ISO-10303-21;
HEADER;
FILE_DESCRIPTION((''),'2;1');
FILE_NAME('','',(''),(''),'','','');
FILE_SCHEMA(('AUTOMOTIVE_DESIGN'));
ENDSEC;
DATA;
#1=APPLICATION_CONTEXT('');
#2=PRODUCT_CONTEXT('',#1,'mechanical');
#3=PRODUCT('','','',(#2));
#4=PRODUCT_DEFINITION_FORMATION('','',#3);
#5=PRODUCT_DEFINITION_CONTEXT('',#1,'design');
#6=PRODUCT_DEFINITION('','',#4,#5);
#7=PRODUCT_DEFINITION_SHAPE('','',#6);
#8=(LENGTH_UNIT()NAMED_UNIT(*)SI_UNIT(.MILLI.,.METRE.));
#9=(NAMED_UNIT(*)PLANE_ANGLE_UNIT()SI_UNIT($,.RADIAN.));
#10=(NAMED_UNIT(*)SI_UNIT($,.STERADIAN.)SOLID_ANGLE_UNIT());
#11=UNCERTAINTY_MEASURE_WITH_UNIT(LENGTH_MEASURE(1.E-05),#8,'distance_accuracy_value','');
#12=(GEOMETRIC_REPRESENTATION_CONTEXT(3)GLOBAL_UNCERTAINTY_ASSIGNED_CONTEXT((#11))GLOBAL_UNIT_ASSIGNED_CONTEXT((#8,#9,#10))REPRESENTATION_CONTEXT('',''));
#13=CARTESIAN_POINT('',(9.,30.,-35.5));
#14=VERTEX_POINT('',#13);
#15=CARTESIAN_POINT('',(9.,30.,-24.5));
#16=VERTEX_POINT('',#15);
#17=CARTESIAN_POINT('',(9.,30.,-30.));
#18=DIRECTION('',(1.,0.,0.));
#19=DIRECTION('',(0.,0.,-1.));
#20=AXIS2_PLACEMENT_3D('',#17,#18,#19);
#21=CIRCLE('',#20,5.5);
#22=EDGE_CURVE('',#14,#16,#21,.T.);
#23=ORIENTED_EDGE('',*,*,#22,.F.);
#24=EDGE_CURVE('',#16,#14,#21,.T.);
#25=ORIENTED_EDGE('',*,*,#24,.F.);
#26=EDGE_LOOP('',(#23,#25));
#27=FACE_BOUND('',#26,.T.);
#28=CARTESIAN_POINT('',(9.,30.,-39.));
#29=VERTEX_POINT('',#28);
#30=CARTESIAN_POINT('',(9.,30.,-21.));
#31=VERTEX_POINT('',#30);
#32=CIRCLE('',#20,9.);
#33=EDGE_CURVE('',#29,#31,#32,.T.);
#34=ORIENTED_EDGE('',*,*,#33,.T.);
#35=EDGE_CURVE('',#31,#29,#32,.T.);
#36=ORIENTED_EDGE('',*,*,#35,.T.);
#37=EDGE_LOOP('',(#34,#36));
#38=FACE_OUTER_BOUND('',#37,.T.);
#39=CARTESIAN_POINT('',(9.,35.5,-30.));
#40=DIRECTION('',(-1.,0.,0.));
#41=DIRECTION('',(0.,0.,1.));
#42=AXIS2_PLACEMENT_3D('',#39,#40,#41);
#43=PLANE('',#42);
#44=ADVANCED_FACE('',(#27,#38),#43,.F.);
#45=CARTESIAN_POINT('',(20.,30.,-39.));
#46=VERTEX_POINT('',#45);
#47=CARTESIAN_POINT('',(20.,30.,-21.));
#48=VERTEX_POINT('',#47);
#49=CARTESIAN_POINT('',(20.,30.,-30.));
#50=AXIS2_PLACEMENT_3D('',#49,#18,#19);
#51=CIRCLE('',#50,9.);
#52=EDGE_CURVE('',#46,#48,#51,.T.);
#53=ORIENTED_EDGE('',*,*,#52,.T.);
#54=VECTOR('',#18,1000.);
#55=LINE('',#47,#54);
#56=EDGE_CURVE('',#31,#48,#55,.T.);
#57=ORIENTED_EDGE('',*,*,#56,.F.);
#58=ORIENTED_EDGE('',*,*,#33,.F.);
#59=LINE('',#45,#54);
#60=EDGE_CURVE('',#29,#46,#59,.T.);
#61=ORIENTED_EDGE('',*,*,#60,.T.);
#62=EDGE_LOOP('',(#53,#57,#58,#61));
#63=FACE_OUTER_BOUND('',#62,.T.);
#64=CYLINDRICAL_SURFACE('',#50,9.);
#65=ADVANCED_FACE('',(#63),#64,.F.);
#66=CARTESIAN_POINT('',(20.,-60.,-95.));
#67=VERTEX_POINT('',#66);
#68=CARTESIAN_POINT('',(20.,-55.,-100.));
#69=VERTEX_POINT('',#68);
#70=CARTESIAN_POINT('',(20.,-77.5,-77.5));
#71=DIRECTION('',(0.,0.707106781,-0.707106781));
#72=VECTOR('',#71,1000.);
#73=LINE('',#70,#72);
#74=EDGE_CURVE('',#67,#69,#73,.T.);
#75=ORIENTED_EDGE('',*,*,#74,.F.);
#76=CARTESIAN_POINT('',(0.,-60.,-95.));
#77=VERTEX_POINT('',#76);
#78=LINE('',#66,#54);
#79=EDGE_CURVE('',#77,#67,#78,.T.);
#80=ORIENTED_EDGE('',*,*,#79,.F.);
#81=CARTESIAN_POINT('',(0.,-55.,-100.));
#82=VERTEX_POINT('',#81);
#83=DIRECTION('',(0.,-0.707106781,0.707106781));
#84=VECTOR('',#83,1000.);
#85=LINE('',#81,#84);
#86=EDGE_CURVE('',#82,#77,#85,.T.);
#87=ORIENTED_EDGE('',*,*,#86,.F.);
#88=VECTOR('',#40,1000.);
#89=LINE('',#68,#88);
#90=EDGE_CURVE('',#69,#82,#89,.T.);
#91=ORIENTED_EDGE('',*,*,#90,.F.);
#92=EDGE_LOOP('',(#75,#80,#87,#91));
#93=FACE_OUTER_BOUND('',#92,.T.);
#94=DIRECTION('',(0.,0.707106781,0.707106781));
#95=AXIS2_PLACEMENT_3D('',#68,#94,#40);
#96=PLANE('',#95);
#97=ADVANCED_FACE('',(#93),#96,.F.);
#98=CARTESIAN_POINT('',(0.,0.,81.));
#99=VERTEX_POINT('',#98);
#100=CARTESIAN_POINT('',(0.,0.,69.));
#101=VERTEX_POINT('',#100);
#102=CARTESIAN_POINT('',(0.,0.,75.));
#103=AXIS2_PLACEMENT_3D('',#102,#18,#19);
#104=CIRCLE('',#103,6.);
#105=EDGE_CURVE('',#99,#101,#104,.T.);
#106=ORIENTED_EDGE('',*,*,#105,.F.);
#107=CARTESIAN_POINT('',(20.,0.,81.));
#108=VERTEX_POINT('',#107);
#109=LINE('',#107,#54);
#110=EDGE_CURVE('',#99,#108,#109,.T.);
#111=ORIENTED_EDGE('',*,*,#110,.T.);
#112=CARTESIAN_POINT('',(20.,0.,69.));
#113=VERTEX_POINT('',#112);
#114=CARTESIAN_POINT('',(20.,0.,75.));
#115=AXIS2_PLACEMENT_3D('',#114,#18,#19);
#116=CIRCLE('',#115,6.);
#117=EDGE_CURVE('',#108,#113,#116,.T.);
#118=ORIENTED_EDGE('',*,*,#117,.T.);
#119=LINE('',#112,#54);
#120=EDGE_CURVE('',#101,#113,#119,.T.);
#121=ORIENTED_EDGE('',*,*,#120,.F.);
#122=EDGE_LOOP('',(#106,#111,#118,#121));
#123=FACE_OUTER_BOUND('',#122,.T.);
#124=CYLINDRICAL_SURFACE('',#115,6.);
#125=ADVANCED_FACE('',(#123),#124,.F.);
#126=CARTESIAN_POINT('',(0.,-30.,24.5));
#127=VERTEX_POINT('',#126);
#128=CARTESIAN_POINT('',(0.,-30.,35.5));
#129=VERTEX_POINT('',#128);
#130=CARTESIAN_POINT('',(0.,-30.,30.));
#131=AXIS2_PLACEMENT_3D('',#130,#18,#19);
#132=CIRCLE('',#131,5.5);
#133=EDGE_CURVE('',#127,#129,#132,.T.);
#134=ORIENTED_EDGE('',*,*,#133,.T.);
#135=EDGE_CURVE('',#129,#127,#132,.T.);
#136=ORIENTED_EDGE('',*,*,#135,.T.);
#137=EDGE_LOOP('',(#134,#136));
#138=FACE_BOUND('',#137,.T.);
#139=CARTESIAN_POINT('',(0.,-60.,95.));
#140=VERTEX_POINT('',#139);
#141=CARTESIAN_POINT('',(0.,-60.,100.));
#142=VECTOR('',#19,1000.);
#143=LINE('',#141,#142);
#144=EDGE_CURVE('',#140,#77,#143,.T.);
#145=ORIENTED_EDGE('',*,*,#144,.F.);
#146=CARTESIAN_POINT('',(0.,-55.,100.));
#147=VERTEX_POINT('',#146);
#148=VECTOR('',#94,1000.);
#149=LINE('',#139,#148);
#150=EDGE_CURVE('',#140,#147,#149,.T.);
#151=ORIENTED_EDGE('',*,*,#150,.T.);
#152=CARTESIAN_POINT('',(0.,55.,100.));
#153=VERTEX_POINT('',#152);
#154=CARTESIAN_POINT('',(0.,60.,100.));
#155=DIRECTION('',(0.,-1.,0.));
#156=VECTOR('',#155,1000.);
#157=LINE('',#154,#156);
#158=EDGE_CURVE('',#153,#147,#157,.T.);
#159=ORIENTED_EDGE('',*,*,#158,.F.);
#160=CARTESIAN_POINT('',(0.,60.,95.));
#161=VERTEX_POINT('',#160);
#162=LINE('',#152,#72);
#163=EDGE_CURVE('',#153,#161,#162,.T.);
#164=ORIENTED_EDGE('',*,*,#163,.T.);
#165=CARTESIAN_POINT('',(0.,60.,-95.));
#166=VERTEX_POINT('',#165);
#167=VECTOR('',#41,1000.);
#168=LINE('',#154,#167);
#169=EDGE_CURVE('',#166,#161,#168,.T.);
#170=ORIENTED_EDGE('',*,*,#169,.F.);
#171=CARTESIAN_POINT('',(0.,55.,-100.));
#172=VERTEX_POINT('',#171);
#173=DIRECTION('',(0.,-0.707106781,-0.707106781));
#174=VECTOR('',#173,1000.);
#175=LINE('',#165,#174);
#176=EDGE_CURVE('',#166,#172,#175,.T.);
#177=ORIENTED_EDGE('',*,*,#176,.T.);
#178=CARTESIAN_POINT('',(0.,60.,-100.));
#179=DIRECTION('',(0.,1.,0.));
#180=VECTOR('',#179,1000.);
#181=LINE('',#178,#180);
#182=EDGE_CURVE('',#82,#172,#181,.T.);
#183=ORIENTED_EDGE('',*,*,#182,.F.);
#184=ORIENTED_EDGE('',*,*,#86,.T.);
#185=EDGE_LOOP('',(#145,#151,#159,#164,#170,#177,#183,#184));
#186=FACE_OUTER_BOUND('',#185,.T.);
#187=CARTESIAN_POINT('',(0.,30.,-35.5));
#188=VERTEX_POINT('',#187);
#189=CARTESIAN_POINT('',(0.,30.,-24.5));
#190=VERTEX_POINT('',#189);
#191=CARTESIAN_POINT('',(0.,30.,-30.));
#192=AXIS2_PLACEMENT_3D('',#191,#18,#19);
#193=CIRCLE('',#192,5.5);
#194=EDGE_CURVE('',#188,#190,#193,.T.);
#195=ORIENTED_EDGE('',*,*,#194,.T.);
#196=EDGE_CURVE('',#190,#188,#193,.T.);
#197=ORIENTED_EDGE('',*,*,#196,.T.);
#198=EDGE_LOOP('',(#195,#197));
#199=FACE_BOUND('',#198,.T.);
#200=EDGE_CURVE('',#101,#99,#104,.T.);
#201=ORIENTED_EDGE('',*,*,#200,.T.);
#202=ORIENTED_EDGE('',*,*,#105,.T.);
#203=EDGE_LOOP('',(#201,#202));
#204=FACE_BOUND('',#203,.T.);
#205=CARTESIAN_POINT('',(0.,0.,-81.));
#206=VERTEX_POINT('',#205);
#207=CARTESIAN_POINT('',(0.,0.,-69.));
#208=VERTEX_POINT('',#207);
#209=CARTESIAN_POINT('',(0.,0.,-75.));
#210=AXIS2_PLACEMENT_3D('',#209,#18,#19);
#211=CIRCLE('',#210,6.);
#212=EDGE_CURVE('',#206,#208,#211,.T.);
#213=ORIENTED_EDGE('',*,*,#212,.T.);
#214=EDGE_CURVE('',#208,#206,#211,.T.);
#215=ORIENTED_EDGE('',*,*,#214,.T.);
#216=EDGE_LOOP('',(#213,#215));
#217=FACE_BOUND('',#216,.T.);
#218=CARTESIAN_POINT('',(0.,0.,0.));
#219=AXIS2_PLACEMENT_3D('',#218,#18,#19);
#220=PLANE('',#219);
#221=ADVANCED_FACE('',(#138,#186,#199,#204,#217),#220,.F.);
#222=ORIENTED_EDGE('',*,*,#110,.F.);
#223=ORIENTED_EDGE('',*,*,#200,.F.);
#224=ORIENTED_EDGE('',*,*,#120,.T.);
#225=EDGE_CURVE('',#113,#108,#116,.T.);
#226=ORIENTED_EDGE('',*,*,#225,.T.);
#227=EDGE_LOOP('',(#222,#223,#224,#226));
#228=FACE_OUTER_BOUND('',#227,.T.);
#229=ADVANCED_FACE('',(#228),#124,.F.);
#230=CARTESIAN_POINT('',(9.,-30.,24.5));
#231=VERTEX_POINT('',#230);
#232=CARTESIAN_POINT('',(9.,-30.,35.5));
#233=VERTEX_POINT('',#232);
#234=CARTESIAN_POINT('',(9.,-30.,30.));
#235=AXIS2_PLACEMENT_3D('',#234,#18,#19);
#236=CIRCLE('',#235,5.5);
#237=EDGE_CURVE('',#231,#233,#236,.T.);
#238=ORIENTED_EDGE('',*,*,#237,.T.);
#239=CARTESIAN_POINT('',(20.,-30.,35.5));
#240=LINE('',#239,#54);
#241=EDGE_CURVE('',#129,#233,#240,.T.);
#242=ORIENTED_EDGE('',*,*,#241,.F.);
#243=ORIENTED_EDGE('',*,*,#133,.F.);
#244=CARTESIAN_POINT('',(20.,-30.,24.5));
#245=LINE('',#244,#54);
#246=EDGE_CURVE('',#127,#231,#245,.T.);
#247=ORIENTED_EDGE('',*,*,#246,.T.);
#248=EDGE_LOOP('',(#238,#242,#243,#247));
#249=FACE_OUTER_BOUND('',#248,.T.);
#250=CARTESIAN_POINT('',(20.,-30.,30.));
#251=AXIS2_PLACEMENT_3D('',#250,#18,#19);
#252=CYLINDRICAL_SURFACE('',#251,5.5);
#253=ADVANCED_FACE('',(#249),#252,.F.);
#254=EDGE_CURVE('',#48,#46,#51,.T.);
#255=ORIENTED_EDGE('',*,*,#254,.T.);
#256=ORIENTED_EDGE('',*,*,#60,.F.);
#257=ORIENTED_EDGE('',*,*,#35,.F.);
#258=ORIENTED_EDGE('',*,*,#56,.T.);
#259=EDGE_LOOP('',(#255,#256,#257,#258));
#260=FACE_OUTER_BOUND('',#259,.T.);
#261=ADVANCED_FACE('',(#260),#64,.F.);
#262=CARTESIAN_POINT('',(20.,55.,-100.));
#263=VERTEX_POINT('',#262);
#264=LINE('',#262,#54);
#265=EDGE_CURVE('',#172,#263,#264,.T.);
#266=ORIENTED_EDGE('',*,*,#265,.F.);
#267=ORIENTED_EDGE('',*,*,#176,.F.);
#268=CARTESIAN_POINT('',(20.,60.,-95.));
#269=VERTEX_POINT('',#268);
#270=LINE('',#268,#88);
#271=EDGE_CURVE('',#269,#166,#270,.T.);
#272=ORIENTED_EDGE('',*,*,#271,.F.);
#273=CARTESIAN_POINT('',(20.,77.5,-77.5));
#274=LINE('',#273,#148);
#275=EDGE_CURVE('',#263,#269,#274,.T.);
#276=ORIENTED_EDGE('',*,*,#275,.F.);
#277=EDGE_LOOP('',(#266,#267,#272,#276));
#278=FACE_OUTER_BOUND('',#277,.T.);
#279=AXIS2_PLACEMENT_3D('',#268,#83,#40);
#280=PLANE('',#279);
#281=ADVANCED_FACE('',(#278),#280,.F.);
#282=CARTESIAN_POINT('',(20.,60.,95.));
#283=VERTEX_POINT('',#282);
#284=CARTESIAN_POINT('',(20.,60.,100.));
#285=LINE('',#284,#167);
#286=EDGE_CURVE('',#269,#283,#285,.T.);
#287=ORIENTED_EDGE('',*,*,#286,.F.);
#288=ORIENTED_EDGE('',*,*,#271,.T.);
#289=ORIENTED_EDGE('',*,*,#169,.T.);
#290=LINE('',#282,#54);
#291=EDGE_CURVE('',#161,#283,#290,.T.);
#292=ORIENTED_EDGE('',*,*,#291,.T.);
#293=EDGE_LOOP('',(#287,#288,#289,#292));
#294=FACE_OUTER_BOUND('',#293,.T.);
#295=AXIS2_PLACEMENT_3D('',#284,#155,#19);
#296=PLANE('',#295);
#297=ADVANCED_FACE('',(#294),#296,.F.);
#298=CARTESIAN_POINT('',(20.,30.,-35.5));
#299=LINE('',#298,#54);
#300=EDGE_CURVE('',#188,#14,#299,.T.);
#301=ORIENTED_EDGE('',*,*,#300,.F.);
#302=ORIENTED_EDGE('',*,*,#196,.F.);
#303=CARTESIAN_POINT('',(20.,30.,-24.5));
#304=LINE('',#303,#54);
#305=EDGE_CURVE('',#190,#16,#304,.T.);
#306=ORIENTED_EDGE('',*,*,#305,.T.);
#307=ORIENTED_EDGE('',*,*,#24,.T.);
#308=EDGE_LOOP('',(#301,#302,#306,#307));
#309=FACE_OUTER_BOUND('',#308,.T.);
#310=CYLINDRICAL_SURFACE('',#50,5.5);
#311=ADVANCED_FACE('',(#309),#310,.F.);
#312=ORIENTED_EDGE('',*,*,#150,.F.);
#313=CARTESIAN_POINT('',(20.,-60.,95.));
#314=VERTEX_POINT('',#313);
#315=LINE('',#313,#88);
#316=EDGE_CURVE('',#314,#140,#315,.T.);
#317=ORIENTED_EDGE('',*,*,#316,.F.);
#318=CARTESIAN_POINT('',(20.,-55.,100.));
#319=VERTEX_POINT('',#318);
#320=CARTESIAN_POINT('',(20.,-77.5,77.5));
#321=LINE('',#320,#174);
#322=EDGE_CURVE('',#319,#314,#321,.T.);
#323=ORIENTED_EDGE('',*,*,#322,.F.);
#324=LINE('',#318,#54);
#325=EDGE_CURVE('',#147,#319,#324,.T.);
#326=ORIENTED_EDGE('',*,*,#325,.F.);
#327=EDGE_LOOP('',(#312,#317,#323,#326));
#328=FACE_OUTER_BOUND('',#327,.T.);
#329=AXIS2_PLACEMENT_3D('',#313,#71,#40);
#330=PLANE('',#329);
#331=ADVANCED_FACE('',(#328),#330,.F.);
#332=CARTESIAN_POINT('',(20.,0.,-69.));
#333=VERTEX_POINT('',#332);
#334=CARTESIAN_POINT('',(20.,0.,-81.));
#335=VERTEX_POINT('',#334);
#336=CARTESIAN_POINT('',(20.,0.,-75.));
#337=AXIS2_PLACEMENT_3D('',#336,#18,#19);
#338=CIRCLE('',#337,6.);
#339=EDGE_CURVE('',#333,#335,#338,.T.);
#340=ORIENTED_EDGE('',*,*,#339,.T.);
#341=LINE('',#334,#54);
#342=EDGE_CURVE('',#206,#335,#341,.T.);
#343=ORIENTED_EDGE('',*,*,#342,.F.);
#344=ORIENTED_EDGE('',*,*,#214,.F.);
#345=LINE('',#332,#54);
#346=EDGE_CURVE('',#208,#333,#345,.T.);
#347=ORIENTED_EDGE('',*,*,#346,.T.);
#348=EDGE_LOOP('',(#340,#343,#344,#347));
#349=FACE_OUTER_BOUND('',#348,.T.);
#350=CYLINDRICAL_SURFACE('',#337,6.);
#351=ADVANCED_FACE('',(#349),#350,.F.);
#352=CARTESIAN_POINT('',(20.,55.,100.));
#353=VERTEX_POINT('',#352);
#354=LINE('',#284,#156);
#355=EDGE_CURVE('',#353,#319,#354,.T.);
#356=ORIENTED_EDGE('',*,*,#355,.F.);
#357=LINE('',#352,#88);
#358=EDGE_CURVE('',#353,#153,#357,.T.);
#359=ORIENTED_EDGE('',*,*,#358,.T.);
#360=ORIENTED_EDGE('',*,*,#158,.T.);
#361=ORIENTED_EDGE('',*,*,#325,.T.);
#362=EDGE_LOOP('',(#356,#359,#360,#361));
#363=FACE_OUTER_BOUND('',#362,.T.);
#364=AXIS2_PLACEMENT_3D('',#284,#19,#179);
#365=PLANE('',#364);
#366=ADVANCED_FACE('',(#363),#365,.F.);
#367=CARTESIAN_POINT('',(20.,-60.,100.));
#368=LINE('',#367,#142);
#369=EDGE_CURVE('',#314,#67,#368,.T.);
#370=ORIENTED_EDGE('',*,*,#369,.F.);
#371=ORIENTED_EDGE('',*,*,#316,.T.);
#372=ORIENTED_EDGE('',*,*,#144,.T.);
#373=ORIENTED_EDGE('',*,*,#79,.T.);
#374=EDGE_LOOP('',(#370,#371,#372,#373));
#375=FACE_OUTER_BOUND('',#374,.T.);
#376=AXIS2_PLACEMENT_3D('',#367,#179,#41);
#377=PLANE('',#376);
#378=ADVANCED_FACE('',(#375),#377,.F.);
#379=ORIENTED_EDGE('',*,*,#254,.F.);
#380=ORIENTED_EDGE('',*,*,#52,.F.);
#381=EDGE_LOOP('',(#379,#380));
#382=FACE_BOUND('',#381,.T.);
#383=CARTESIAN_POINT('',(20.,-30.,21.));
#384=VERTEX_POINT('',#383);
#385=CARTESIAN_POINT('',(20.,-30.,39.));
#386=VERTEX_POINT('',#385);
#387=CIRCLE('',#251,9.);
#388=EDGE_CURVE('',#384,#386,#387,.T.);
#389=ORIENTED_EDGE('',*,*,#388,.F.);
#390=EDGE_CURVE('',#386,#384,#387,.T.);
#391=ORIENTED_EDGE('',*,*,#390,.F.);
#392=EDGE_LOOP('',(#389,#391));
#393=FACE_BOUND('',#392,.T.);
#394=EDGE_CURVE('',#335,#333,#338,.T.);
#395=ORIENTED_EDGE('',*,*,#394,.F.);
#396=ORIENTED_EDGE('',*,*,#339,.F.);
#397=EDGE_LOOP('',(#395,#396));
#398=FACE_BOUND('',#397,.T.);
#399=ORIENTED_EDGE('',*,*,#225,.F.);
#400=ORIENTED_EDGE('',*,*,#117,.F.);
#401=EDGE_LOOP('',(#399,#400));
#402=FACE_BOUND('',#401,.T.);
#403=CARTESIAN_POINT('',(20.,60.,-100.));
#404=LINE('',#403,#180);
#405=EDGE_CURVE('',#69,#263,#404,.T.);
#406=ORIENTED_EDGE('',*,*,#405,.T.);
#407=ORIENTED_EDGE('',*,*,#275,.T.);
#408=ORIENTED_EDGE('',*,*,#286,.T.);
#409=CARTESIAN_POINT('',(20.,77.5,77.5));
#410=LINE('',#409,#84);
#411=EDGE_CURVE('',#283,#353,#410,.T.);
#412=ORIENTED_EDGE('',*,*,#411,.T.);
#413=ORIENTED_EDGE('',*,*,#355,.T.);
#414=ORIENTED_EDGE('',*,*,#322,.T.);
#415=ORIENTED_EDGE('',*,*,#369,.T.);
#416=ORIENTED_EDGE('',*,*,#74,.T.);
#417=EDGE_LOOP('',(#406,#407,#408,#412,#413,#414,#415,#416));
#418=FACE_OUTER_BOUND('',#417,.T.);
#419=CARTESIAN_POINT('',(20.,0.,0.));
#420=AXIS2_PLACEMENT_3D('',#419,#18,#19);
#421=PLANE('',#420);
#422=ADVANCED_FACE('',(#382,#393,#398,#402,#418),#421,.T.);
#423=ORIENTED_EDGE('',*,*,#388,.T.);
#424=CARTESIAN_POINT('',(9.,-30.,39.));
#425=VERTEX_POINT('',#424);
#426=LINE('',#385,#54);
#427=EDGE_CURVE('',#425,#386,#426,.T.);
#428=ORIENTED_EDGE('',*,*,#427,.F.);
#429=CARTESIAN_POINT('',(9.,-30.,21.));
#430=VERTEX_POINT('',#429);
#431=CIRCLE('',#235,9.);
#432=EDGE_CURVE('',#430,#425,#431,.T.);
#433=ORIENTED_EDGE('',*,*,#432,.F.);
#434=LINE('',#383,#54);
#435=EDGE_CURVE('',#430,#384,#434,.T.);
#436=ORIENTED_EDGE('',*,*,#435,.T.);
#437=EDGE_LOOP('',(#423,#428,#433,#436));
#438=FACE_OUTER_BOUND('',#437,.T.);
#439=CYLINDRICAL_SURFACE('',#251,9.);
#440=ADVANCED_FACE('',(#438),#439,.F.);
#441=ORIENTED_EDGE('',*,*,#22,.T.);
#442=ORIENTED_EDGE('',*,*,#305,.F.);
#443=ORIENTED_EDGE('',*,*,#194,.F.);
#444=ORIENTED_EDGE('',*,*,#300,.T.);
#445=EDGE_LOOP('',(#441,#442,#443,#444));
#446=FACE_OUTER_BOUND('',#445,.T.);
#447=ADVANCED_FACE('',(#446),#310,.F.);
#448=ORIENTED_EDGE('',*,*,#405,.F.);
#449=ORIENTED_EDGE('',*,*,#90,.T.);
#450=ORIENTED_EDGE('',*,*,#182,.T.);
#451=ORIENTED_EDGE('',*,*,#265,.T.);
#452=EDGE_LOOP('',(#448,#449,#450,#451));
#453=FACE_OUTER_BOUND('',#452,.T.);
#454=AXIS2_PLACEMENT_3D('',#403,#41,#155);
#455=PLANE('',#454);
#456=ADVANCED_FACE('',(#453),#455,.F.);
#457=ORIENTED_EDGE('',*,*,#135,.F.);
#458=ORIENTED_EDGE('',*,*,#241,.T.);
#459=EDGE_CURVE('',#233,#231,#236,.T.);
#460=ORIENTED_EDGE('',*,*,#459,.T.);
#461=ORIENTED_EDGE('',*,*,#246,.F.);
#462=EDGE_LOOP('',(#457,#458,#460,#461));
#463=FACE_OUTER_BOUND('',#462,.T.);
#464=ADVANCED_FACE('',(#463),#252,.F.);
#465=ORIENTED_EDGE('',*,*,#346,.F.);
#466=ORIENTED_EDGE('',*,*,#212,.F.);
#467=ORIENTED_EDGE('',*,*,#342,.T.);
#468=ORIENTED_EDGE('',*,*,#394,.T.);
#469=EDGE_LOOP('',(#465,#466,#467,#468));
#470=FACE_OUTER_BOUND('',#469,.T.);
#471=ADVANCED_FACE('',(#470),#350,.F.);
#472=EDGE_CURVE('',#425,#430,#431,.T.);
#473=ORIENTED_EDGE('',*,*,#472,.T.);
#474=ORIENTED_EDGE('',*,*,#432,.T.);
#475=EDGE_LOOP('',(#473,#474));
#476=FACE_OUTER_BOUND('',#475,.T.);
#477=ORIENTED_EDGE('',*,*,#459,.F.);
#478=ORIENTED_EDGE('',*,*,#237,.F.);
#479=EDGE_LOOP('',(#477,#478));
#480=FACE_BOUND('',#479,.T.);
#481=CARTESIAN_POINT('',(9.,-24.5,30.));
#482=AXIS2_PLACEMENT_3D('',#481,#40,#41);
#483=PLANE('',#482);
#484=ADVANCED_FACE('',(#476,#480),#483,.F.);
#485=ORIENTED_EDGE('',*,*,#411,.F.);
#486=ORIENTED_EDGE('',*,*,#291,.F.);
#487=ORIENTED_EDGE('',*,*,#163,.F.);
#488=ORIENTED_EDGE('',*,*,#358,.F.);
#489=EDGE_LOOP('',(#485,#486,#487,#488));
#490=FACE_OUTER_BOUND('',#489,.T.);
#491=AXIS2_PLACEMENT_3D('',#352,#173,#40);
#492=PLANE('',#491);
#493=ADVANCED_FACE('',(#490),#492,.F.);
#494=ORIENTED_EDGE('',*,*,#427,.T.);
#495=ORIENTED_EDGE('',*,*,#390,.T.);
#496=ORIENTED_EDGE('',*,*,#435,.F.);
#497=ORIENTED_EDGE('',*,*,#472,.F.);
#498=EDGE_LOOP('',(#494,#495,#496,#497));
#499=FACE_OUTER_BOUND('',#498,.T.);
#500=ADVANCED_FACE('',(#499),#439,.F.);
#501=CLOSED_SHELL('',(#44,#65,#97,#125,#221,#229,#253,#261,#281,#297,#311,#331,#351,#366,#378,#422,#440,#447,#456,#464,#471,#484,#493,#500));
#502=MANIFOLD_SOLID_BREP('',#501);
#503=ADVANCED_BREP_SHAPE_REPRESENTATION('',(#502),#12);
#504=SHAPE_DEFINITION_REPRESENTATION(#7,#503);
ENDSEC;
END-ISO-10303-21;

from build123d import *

# Parameters (mm, degrees)
SKETCH_1_W                = 200
SKETCH_1_H                = 120
EXTRUDE_1_DEPTH           = 20
HOLE_WIZARD_1_D           = 11
HOLE_WIZARD_1_CBORE_D     = 18
HOLE_WIZARD_1_CBORE_DEPTH = 11
HOLE_WIZARD_M14_1_D       = 12
CHAMFER_1_SIZE            = 5


with BuildPart() as part:
    # 草图1 → 凸台-拉伸1 (new body)
    with BuildSketch(Plane(origin=(0, 0, 0), x_dir=(0, 0, -1), z_dir=(1, 0, 0))):
        Rectangle(SKETCH_1_W, SKETCH_1_H)
    extrude(amount=EXTRUDE_1_DEPTH)

    # 打孔尺寸(%根据)内六角圆柱头螺钉的类型1 (through all)
    with Locations(Plane(origin=(20, 0, 0), x_dir=(0, 0, -1), z_dir=(1, 0, 0))):
        with Locations((30, 30), (-30, -30)):
            CounterBoreHole(HOLE_WIZARD_1_D / 2, HOLE_WIZARD_1_CBORE_D / 2, HOLE_WIZARD_1_CBORE_DEPTH)

    # M14 螺纹孔1 (through all)
    with Locations(Plane(origin=(20, 0, 0), x_dir=(0, 0, -1), z_dir=(1, 0, 0))):
        with Locations((-75, 0), (75, 0)):
            Hole(HOLE_WIZARD_M14_1_D / 2)

    # 倒角1
    chamfer_1_edges = [part.edges().sort_by_distance(p)[0] for p in [
        (10, -60, -100),
        (10, -60, 100),
        (10, 60, 100),
        (10, 60, -100),
    ]]
    chamfer(chamfer_1_edges, length=CHAMFER_1_SIZE)


solid = part.part
